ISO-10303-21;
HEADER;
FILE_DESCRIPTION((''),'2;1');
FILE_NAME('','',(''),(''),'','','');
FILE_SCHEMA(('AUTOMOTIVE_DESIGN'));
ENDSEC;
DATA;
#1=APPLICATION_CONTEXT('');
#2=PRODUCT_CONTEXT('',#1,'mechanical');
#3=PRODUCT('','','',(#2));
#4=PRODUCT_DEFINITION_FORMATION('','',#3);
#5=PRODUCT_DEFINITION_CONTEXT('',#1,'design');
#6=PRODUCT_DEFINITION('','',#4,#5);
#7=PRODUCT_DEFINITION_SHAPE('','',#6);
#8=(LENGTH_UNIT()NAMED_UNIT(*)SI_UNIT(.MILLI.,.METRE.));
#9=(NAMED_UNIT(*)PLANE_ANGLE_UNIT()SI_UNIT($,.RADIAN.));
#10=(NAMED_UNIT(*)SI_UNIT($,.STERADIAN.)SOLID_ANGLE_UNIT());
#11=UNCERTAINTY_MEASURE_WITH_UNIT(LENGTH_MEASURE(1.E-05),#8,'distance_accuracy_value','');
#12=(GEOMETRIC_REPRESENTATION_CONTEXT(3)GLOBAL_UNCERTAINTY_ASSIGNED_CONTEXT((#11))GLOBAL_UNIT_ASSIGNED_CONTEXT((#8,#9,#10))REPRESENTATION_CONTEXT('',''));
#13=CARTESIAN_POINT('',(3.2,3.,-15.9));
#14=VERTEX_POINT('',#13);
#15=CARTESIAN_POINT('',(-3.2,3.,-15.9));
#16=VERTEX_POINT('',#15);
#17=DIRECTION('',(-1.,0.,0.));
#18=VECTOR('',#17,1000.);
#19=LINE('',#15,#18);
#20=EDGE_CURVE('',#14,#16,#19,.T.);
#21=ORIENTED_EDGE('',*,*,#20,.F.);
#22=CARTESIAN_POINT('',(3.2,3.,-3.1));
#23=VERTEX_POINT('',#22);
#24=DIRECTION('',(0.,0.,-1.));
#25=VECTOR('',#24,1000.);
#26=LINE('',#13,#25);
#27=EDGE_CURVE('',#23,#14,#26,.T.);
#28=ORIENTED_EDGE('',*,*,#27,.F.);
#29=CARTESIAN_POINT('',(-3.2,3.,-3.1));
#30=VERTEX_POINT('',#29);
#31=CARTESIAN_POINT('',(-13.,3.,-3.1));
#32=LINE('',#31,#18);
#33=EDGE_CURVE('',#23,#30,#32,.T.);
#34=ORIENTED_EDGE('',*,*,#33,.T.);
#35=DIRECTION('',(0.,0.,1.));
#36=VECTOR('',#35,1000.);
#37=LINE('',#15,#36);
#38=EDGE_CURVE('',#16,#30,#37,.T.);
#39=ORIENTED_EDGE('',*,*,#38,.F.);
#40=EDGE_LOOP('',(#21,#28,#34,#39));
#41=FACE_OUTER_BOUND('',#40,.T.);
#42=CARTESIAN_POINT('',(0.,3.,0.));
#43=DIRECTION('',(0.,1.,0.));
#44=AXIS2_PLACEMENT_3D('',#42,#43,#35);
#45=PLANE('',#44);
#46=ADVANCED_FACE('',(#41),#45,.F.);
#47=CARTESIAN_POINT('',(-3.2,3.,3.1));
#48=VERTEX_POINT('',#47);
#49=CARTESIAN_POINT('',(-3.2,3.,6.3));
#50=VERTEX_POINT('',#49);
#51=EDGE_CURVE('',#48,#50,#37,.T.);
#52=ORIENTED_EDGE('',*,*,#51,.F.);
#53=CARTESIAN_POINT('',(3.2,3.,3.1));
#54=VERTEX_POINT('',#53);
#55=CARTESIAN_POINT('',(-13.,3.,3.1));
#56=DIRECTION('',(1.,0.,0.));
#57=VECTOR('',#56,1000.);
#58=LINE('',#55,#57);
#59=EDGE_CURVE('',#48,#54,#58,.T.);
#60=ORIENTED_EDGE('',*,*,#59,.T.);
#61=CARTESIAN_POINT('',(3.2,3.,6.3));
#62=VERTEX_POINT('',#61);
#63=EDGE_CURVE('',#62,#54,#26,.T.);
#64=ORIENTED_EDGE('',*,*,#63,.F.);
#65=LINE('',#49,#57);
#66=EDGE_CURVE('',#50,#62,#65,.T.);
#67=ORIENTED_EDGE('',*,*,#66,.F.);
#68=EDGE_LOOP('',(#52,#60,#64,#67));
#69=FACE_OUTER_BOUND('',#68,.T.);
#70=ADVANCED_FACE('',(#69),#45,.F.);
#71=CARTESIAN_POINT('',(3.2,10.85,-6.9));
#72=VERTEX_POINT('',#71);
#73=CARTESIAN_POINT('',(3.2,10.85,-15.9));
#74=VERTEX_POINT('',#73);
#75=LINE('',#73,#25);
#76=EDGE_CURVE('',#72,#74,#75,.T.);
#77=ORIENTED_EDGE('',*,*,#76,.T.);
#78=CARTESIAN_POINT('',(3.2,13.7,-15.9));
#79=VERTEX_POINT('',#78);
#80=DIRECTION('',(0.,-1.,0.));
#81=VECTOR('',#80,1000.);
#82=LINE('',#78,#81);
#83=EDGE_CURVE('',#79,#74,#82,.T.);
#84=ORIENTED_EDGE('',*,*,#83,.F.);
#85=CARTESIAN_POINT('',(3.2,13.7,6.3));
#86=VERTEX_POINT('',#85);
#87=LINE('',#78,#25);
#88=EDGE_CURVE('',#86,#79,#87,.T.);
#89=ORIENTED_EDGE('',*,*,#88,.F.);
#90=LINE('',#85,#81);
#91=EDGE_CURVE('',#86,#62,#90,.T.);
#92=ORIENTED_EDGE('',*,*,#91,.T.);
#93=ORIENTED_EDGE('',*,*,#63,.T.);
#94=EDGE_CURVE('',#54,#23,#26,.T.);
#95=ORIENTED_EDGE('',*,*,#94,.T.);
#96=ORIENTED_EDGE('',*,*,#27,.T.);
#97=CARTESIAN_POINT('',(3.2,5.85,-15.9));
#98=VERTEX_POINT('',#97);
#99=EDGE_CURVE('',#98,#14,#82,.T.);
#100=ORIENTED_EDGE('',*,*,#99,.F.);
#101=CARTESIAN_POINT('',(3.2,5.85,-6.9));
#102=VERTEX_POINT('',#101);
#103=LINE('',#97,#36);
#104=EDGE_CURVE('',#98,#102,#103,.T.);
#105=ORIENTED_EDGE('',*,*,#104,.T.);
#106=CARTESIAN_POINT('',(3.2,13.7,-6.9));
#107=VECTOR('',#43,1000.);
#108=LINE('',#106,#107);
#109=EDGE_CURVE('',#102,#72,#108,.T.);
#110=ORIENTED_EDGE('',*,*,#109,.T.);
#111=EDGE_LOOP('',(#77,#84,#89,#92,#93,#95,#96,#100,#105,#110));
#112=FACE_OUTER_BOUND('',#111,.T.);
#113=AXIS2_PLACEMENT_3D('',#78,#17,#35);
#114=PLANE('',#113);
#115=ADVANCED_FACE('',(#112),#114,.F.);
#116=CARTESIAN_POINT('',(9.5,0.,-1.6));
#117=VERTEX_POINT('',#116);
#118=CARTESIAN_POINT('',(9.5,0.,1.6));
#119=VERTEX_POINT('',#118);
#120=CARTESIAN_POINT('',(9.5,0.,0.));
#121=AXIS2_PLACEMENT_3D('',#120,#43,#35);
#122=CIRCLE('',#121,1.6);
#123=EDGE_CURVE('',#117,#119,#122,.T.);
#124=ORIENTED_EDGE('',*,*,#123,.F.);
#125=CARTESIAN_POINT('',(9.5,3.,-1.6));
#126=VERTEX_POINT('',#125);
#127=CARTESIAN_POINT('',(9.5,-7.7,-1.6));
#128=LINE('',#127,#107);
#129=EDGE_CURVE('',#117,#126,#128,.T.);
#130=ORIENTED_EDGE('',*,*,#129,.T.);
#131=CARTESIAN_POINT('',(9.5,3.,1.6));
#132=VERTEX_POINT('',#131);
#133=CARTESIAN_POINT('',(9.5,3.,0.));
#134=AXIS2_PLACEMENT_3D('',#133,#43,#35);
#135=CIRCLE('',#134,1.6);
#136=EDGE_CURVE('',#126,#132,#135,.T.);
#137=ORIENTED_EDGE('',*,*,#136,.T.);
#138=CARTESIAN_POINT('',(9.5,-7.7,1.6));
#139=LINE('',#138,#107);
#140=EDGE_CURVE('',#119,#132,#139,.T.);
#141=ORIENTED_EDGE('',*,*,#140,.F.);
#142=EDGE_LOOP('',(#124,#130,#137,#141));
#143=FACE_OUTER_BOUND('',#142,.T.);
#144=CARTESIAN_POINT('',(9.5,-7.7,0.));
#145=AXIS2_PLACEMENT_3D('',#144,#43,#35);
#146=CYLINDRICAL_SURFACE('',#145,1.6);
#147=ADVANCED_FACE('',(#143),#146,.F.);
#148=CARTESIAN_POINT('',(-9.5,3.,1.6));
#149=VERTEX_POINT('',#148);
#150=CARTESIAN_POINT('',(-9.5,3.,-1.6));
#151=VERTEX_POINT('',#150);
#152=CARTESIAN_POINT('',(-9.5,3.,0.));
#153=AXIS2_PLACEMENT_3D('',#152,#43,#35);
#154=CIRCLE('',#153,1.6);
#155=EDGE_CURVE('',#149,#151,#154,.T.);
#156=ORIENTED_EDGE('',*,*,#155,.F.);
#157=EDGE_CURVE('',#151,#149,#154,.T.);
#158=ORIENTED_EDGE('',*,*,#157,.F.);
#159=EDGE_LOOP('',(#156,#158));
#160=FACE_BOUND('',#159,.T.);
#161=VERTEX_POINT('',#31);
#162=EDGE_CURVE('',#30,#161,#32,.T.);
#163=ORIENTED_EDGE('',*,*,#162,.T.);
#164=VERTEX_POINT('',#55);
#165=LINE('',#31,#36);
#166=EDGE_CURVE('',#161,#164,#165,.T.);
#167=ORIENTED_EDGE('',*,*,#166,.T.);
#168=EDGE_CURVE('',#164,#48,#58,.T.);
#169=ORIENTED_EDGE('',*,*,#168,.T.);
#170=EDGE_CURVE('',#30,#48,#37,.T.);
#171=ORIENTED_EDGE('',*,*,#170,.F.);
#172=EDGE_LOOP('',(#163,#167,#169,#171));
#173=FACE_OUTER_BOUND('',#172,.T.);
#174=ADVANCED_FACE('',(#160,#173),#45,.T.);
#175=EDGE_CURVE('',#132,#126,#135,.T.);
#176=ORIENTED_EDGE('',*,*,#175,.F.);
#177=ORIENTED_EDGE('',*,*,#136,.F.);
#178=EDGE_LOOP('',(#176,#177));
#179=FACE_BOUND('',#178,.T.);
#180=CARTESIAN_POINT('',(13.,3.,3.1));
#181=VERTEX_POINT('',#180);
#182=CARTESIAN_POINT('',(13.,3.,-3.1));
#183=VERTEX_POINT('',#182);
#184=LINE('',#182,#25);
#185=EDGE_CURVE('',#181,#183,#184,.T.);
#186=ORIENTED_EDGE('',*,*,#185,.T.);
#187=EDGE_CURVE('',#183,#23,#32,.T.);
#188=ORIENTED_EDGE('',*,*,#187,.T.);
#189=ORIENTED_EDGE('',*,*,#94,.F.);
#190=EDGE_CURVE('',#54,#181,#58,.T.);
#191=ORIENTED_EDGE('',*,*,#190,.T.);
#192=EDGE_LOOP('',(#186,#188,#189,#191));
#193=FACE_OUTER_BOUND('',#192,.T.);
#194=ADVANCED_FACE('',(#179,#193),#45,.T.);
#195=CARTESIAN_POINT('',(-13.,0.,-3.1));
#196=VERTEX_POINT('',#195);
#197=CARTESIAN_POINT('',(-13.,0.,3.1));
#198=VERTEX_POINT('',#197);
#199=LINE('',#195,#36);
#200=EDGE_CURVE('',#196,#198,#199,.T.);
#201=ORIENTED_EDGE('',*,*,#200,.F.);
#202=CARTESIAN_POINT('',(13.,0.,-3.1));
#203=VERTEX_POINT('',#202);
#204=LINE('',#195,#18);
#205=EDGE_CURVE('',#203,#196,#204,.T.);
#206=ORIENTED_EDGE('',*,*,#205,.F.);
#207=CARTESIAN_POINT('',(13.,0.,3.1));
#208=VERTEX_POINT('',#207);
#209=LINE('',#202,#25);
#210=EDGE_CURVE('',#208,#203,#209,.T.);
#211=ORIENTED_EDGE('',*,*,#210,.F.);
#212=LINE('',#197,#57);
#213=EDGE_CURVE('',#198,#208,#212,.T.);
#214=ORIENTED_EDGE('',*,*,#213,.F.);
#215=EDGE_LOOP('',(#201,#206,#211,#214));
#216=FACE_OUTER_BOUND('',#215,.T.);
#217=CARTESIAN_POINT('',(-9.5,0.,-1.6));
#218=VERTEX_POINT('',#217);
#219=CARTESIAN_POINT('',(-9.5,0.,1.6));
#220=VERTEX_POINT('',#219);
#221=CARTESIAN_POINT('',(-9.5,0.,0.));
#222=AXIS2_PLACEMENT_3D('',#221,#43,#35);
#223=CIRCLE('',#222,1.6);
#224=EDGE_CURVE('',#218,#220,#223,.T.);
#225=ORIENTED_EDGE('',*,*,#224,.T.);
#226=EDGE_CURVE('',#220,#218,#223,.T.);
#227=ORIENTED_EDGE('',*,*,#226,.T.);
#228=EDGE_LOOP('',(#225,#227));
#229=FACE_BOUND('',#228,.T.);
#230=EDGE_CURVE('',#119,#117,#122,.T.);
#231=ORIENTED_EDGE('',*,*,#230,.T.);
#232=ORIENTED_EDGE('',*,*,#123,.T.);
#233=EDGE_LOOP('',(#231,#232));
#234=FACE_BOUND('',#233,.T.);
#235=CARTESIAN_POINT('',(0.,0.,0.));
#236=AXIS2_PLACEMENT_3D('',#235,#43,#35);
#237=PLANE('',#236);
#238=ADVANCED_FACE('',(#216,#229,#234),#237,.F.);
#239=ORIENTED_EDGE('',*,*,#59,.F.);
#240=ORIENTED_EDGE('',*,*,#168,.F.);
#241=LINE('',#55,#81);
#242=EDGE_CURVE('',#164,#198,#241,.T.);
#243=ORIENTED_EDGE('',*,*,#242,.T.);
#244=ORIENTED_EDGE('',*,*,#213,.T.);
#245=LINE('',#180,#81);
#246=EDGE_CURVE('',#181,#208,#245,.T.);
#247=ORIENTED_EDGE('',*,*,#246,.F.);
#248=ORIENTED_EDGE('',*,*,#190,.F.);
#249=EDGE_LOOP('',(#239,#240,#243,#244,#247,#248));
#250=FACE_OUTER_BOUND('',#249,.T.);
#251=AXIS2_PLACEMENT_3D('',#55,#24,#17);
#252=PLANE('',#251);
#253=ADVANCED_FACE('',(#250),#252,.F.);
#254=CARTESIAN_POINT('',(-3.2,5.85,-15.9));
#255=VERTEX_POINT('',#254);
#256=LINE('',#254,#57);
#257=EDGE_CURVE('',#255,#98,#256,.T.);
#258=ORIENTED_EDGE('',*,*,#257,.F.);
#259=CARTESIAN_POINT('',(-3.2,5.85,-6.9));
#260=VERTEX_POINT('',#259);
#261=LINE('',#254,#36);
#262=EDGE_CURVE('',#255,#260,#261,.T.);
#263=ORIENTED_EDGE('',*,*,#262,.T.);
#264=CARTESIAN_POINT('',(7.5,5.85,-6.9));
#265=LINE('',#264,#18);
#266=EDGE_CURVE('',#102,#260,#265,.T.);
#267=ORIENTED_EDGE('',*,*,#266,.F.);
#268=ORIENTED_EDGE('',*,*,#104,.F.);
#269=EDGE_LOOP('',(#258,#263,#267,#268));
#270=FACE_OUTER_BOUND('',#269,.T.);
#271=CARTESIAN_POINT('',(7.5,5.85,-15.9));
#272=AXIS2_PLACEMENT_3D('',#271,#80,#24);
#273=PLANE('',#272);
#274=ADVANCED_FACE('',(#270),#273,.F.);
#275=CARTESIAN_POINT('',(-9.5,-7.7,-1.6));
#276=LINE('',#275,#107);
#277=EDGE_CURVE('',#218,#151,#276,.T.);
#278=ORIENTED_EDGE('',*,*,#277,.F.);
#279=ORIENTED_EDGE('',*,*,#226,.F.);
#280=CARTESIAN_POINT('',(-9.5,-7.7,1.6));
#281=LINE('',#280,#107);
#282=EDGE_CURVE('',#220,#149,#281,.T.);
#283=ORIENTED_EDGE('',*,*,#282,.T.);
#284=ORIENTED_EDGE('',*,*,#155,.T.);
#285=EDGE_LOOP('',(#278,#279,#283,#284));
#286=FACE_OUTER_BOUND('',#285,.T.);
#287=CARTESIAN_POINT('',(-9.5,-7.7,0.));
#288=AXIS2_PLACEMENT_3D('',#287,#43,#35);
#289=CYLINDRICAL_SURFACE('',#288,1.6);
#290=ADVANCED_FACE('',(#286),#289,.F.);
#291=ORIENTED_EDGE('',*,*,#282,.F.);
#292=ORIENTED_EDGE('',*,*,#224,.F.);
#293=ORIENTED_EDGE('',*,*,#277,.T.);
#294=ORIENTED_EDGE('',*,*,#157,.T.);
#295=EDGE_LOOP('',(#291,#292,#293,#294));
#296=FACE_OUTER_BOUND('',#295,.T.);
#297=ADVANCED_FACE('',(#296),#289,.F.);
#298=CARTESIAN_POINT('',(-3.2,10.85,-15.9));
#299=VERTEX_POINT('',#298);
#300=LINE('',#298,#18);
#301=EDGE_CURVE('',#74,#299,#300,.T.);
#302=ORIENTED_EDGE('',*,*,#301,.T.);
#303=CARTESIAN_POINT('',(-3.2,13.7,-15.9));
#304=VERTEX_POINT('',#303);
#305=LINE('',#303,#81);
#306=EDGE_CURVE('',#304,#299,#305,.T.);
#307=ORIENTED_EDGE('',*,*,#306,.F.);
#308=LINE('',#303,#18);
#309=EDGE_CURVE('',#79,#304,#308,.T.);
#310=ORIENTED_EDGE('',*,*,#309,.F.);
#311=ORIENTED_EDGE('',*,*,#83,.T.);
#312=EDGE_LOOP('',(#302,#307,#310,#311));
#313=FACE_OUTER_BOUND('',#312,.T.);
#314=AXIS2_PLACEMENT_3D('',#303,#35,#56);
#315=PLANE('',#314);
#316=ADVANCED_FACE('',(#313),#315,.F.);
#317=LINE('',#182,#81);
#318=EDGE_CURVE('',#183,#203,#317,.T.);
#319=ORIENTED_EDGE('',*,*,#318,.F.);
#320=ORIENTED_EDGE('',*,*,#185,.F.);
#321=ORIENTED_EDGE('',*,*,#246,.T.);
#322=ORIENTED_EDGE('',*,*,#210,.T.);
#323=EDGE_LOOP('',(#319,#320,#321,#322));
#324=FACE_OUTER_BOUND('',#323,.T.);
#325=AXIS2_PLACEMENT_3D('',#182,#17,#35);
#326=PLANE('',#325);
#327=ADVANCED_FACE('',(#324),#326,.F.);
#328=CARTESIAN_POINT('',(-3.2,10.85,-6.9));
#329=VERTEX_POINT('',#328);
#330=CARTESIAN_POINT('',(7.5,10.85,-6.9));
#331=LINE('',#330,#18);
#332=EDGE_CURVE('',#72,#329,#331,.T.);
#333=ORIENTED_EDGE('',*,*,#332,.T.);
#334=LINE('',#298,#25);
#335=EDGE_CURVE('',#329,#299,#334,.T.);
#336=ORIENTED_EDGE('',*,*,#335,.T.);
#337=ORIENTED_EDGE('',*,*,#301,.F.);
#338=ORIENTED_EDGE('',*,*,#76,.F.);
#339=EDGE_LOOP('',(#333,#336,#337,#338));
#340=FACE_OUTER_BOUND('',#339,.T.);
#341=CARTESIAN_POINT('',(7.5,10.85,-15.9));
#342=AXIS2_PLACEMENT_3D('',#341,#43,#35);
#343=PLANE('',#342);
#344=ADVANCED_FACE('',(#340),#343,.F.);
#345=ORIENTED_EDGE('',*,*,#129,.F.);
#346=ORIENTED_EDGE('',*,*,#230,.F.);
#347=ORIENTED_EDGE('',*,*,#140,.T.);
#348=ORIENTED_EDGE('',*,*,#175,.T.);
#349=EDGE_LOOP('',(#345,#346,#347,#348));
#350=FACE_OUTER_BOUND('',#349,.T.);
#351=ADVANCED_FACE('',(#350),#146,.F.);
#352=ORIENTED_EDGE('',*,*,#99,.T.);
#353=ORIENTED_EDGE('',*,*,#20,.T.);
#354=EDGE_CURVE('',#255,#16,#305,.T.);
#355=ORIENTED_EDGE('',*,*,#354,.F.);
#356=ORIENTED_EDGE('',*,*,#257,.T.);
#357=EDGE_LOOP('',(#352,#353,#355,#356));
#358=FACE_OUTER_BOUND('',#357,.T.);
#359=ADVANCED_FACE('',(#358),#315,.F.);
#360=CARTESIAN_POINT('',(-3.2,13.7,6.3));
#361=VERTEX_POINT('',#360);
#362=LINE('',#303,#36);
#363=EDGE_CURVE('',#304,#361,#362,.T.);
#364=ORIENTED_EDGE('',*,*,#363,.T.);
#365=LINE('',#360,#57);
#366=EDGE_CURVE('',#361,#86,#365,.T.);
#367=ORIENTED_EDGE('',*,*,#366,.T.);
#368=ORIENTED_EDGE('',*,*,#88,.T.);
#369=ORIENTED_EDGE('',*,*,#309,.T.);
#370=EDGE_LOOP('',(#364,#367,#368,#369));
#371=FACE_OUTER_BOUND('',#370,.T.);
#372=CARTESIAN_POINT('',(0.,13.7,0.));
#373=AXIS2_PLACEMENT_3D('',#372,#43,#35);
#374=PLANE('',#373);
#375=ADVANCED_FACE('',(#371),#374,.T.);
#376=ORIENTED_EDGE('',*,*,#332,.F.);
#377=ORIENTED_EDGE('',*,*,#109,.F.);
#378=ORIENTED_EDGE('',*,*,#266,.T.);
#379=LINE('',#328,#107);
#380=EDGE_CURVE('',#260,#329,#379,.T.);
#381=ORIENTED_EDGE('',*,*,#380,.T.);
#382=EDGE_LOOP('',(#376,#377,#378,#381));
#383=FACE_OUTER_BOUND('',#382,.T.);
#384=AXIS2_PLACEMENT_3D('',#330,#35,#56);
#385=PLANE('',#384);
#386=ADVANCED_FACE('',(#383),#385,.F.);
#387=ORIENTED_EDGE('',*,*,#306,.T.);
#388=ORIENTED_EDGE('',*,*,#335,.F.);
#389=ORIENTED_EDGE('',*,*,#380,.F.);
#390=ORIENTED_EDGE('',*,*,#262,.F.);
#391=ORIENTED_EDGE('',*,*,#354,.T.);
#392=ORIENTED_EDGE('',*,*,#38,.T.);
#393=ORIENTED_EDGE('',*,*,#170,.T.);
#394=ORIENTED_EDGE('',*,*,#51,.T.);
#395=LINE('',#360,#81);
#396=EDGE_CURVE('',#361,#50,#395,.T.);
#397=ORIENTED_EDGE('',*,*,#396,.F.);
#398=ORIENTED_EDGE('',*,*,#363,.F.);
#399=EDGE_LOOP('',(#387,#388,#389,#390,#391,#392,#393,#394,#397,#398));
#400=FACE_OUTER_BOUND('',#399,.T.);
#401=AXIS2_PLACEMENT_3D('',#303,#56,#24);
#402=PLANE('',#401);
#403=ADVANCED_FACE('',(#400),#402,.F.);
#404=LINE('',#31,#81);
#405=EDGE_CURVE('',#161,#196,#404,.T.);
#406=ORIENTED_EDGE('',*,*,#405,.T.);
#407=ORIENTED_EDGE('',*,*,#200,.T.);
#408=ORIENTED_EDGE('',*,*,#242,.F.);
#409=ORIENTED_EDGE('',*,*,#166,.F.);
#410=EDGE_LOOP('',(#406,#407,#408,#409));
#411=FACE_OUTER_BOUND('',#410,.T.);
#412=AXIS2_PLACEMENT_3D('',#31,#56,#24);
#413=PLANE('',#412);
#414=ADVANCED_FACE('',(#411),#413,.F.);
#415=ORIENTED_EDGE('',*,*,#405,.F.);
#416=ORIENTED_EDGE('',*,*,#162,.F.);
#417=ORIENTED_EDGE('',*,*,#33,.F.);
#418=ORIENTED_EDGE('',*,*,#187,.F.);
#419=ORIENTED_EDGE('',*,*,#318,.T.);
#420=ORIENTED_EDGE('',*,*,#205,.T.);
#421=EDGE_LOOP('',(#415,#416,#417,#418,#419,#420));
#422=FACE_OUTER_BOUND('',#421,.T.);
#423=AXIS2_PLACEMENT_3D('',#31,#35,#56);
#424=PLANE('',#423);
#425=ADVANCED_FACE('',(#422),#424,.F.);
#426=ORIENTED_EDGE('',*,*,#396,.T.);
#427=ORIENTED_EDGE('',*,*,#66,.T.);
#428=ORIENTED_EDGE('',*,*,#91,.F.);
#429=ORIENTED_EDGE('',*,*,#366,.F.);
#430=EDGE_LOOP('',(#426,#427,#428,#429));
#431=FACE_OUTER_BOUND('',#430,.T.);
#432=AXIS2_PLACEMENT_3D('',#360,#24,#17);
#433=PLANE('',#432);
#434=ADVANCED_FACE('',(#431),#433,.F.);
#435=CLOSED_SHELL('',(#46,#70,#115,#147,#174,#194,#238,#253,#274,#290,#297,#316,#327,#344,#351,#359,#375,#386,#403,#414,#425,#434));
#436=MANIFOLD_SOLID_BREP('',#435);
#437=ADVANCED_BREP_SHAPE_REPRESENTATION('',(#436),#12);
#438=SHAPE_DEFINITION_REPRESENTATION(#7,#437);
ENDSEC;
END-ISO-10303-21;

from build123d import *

# Parameters (mm, degrees)
SKETCH_1_W          = 26
SKETCH_1_H          = 6.2
EXTRUDE_1_DEPTH     = 3
SKETCH_2_W          = 6.4
SKETCH_2_H          = 22.2
EXTRUDE_2_DEPTH     = 10.7
SKETCH_3_W          = 9
SKETCH_3_H          = 5
CUT_EXTRUDE_1_DEPTH = 10.7
SKETCH_4_R          = 1.6
CUT_EXTRUDE_2_DEPTH = 10.7


with BuildPart() as part:
    # 草图1 → 凸台-拉伸1 (new body)
    with BuildSketch(Plane(origin=(0, 0, 0), x_dir=(1, 0, 0), z_dir=(0, 1, 0))):
        Rectangle(SKETCH_1_W, SKETCH_1_H)
    extrude(amount=EXTRUDE_1_DEPTH)

    # 草图2 → 凸台-拉伸2 (add)
    with BuildSketch(Plane(origin=(0, 3, 0), x_dir=(1, 0, 0), z_dir=(0, 1, 0))):
        with Locations((0, 4.8)):
            Rectangle(SKETCH_2_W, SKETCH_2_H)
    extrude(amount=EXTRUDE_2_DEPTH)

    # 草图3 → 切除-拉伸1 (cut)
    with BuildSketch(Plane.ZY.offset(3.2)):
        with Locations((-11.4, 8.35)):
            Rectangle(SKETCH_3_W, SKETCH_3_H)
    extrude(amount=-CUT_EXTRUDE_1_DEPTH, mode=Mode.SUBTRACT)

    # 草图4 → 切除-拉伸2 (cut)
    with BuildSketch(Plane(origin=(0, 3, 0), x_dir=(1, 0, 0), z_dir=(0, 1, 0))):
        with Locations(Location((-9.5, 0, 0), (0, 0, 270))):
            Circle(SKETCH_4_R)
        with Locations(Location((9.5, 0, 0), (0, 0, 270))):
            Circle(SKETCH_4_R)
    extrude(amount=-CUT_EXTRUDE_2_DEPTH, mode=Mode.SUBTRACT)


solid = part.part
